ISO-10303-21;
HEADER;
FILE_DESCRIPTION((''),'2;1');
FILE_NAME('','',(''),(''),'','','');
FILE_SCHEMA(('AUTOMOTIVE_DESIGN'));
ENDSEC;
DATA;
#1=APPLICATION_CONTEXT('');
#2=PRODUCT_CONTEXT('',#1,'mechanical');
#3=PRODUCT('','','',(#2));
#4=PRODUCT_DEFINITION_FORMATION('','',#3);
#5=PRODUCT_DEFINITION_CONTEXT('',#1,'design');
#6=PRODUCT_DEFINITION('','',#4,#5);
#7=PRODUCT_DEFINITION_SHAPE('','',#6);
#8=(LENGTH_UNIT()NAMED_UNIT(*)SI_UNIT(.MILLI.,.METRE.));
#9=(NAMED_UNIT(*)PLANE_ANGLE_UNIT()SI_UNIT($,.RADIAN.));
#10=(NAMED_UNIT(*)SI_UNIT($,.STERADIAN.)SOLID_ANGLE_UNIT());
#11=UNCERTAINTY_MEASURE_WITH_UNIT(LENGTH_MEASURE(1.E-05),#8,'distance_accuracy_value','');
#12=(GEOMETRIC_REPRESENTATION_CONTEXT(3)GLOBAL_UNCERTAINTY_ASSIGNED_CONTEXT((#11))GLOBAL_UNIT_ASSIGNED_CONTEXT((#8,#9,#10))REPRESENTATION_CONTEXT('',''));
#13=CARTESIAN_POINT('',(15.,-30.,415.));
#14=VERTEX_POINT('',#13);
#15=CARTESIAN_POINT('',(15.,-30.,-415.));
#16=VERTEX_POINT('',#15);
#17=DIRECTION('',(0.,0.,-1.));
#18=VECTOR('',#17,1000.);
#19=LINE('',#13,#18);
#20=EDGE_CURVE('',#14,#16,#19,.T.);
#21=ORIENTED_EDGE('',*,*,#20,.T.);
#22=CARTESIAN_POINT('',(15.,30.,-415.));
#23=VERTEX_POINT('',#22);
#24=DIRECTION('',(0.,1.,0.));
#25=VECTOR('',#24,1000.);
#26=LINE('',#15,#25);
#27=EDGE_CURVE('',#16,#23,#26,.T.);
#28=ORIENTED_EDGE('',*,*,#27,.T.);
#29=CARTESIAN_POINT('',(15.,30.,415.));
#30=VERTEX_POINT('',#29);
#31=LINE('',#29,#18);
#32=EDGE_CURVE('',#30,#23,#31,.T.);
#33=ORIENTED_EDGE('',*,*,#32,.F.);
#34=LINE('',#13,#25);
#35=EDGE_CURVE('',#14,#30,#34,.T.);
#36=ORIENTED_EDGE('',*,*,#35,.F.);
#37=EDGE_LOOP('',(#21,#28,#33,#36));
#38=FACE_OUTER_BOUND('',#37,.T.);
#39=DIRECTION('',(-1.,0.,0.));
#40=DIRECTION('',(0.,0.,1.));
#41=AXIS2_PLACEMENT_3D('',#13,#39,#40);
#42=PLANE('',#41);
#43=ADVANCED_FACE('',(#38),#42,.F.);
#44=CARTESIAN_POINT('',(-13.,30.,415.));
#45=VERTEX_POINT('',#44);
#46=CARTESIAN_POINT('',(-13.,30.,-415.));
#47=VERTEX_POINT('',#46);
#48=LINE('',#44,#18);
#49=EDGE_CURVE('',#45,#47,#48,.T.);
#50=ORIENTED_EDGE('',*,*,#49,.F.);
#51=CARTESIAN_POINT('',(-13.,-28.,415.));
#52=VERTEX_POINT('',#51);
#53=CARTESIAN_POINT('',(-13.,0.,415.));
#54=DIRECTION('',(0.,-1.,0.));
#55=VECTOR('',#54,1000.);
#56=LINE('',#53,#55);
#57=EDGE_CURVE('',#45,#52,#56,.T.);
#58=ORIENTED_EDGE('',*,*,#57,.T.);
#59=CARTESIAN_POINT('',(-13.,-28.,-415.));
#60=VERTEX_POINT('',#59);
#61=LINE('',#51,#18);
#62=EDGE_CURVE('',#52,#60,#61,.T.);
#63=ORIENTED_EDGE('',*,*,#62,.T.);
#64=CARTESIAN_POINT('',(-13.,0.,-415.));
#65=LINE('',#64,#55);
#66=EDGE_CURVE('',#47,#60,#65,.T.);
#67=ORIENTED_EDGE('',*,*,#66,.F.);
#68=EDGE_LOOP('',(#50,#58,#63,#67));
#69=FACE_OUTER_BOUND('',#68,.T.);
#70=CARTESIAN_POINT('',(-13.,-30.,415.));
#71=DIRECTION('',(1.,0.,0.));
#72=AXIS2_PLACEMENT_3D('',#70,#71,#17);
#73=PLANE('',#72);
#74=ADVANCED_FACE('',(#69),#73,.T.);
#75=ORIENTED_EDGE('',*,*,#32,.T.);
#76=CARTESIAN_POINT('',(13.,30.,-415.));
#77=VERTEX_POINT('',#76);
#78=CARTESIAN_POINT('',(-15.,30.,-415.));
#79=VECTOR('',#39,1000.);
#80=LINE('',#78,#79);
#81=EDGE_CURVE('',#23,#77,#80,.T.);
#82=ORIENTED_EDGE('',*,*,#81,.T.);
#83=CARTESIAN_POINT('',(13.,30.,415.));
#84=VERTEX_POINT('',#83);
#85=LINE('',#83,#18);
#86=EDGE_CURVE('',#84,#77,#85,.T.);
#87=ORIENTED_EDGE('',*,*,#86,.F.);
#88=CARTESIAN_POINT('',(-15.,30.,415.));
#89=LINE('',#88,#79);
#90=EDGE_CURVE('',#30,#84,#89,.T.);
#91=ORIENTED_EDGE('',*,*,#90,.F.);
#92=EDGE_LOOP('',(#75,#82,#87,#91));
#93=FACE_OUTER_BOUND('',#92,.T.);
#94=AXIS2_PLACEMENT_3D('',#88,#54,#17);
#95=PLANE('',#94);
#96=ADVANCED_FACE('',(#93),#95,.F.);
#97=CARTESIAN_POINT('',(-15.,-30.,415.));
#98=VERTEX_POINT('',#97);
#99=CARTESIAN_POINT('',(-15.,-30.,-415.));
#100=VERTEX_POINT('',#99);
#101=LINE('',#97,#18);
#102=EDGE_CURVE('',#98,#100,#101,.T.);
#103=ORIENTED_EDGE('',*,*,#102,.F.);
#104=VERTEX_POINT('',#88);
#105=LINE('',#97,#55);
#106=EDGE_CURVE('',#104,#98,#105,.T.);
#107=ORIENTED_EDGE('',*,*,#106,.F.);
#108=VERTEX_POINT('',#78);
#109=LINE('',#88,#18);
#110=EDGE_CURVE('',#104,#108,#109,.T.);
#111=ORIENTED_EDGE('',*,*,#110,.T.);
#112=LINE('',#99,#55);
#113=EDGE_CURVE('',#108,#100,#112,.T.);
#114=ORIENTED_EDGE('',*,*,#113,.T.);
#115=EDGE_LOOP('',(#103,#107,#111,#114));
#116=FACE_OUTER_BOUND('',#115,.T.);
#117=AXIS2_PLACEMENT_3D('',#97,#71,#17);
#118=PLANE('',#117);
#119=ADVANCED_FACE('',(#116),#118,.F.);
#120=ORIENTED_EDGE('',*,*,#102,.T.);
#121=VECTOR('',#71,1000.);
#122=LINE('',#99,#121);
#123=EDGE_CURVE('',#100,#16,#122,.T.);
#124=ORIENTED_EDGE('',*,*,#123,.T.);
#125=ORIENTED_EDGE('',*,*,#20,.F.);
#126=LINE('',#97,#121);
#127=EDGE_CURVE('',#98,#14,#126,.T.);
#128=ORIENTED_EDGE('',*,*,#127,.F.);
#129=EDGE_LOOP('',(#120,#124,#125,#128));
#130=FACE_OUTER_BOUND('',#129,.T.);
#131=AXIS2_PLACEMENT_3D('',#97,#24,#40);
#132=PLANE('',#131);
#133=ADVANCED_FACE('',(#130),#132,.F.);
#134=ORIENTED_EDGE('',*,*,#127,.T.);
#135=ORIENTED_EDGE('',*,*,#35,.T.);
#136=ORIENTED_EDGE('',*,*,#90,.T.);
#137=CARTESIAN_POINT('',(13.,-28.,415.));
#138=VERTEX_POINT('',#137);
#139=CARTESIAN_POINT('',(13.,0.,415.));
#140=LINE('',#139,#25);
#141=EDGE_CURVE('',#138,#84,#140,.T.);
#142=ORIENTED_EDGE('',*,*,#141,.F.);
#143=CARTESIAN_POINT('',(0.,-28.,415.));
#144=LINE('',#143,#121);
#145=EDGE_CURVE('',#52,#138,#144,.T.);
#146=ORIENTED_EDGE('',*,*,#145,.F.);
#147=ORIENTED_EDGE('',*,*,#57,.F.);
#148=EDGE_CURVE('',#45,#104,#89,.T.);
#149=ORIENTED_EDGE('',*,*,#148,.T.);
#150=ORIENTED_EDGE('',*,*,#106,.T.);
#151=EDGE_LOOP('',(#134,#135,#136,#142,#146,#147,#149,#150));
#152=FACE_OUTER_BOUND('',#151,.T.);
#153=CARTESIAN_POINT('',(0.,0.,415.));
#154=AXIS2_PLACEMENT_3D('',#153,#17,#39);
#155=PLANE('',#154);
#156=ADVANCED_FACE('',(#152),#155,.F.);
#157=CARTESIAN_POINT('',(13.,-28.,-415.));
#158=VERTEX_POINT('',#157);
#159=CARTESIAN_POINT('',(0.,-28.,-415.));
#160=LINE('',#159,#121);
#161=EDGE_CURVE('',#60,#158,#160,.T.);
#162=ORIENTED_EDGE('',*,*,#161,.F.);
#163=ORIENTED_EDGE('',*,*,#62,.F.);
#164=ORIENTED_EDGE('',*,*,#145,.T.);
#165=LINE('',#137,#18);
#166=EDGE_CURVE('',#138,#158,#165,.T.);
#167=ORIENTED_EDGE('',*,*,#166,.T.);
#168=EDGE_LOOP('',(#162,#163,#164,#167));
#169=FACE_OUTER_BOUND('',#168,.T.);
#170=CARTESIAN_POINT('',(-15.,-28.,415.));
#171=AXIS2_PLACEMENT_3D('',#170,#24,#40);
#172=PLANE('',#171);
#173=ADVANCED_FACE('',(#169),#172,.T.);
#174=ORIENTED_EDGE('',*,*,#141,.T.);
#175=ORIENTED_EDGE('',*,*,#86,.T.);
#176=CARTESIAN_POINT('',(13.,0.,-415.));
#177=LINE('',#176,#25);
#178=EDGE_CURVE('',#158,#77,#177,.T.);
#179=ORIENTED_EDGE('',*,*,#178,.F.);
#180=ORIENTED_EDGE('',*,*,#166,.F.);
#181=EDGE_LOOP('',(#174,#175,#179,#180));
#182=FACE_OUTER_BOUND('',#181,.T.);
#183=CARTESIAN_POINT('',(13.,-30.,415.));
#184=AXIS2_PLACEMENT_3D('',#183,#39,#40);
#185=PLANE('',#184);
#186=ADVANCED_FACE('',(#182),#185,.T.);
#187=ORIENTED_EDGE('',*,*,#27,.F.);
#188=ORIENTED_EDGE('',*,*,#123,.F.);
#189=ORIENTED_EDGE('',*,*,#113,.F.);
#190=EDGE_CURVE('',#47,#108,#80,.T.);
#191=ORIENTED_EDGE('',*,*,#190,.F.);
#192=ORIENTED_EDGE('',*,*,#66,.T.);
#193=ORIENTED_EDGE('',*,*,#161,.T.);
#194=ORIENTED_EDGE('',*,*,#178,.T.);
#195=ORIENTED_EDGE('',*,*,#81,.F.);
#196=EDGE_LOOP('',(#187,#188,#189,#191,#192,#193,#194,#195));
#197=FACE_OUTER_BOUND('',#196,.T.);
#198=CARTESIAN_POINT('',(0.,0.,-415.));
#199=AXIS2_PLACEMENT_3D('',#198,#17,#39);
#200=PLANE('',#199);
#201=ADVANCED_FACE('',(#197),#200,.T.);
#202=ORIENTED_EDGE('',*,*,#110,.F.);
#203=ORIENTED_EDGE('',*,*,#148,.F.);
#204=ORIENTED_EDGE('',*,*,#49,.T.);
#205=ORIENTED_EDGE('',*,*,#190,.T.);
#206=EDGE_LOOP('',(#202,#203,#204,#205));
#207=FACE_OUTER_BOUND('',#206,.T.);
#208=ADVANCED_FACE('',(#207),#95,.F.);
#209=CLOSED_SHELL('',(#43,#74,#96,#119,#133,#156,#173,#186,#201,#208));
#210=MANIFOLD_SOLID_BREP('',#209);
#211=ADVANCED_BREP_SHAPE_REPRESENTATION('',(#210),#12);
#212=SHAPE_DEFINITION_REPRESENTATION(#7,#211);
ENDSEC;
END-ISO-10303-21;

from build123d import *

# Parameters (mm, degrees)
SKETCH_1_W      = 30
SKETCH_1_H      = 60
EXTRUDE_1_DEPTH = 415
SHELL_1_T       = -2


with BuildPart() as part:
    # 草图1 → 凸台-拉伸1 (new, symmetric)
    with BuildSketch(Plane.XY):
        Rectangle(SKETCH_1_W, SKETCH_1_H)
    extrude(amount=EXTRUDE_1_DEPTH, both=True)

    # 抽壳1
    shell_1_openings = [part.faces().sort_by_distance(p)[0] for p in [
        (0, 0, 415),
        (0, 0, -415),
        (0, 30, 0),
    ]]
    offset(amount=SHELL_1_T, openings=shell_1_openings, kind=Kind.INTERSECTION)


solid = part.part
